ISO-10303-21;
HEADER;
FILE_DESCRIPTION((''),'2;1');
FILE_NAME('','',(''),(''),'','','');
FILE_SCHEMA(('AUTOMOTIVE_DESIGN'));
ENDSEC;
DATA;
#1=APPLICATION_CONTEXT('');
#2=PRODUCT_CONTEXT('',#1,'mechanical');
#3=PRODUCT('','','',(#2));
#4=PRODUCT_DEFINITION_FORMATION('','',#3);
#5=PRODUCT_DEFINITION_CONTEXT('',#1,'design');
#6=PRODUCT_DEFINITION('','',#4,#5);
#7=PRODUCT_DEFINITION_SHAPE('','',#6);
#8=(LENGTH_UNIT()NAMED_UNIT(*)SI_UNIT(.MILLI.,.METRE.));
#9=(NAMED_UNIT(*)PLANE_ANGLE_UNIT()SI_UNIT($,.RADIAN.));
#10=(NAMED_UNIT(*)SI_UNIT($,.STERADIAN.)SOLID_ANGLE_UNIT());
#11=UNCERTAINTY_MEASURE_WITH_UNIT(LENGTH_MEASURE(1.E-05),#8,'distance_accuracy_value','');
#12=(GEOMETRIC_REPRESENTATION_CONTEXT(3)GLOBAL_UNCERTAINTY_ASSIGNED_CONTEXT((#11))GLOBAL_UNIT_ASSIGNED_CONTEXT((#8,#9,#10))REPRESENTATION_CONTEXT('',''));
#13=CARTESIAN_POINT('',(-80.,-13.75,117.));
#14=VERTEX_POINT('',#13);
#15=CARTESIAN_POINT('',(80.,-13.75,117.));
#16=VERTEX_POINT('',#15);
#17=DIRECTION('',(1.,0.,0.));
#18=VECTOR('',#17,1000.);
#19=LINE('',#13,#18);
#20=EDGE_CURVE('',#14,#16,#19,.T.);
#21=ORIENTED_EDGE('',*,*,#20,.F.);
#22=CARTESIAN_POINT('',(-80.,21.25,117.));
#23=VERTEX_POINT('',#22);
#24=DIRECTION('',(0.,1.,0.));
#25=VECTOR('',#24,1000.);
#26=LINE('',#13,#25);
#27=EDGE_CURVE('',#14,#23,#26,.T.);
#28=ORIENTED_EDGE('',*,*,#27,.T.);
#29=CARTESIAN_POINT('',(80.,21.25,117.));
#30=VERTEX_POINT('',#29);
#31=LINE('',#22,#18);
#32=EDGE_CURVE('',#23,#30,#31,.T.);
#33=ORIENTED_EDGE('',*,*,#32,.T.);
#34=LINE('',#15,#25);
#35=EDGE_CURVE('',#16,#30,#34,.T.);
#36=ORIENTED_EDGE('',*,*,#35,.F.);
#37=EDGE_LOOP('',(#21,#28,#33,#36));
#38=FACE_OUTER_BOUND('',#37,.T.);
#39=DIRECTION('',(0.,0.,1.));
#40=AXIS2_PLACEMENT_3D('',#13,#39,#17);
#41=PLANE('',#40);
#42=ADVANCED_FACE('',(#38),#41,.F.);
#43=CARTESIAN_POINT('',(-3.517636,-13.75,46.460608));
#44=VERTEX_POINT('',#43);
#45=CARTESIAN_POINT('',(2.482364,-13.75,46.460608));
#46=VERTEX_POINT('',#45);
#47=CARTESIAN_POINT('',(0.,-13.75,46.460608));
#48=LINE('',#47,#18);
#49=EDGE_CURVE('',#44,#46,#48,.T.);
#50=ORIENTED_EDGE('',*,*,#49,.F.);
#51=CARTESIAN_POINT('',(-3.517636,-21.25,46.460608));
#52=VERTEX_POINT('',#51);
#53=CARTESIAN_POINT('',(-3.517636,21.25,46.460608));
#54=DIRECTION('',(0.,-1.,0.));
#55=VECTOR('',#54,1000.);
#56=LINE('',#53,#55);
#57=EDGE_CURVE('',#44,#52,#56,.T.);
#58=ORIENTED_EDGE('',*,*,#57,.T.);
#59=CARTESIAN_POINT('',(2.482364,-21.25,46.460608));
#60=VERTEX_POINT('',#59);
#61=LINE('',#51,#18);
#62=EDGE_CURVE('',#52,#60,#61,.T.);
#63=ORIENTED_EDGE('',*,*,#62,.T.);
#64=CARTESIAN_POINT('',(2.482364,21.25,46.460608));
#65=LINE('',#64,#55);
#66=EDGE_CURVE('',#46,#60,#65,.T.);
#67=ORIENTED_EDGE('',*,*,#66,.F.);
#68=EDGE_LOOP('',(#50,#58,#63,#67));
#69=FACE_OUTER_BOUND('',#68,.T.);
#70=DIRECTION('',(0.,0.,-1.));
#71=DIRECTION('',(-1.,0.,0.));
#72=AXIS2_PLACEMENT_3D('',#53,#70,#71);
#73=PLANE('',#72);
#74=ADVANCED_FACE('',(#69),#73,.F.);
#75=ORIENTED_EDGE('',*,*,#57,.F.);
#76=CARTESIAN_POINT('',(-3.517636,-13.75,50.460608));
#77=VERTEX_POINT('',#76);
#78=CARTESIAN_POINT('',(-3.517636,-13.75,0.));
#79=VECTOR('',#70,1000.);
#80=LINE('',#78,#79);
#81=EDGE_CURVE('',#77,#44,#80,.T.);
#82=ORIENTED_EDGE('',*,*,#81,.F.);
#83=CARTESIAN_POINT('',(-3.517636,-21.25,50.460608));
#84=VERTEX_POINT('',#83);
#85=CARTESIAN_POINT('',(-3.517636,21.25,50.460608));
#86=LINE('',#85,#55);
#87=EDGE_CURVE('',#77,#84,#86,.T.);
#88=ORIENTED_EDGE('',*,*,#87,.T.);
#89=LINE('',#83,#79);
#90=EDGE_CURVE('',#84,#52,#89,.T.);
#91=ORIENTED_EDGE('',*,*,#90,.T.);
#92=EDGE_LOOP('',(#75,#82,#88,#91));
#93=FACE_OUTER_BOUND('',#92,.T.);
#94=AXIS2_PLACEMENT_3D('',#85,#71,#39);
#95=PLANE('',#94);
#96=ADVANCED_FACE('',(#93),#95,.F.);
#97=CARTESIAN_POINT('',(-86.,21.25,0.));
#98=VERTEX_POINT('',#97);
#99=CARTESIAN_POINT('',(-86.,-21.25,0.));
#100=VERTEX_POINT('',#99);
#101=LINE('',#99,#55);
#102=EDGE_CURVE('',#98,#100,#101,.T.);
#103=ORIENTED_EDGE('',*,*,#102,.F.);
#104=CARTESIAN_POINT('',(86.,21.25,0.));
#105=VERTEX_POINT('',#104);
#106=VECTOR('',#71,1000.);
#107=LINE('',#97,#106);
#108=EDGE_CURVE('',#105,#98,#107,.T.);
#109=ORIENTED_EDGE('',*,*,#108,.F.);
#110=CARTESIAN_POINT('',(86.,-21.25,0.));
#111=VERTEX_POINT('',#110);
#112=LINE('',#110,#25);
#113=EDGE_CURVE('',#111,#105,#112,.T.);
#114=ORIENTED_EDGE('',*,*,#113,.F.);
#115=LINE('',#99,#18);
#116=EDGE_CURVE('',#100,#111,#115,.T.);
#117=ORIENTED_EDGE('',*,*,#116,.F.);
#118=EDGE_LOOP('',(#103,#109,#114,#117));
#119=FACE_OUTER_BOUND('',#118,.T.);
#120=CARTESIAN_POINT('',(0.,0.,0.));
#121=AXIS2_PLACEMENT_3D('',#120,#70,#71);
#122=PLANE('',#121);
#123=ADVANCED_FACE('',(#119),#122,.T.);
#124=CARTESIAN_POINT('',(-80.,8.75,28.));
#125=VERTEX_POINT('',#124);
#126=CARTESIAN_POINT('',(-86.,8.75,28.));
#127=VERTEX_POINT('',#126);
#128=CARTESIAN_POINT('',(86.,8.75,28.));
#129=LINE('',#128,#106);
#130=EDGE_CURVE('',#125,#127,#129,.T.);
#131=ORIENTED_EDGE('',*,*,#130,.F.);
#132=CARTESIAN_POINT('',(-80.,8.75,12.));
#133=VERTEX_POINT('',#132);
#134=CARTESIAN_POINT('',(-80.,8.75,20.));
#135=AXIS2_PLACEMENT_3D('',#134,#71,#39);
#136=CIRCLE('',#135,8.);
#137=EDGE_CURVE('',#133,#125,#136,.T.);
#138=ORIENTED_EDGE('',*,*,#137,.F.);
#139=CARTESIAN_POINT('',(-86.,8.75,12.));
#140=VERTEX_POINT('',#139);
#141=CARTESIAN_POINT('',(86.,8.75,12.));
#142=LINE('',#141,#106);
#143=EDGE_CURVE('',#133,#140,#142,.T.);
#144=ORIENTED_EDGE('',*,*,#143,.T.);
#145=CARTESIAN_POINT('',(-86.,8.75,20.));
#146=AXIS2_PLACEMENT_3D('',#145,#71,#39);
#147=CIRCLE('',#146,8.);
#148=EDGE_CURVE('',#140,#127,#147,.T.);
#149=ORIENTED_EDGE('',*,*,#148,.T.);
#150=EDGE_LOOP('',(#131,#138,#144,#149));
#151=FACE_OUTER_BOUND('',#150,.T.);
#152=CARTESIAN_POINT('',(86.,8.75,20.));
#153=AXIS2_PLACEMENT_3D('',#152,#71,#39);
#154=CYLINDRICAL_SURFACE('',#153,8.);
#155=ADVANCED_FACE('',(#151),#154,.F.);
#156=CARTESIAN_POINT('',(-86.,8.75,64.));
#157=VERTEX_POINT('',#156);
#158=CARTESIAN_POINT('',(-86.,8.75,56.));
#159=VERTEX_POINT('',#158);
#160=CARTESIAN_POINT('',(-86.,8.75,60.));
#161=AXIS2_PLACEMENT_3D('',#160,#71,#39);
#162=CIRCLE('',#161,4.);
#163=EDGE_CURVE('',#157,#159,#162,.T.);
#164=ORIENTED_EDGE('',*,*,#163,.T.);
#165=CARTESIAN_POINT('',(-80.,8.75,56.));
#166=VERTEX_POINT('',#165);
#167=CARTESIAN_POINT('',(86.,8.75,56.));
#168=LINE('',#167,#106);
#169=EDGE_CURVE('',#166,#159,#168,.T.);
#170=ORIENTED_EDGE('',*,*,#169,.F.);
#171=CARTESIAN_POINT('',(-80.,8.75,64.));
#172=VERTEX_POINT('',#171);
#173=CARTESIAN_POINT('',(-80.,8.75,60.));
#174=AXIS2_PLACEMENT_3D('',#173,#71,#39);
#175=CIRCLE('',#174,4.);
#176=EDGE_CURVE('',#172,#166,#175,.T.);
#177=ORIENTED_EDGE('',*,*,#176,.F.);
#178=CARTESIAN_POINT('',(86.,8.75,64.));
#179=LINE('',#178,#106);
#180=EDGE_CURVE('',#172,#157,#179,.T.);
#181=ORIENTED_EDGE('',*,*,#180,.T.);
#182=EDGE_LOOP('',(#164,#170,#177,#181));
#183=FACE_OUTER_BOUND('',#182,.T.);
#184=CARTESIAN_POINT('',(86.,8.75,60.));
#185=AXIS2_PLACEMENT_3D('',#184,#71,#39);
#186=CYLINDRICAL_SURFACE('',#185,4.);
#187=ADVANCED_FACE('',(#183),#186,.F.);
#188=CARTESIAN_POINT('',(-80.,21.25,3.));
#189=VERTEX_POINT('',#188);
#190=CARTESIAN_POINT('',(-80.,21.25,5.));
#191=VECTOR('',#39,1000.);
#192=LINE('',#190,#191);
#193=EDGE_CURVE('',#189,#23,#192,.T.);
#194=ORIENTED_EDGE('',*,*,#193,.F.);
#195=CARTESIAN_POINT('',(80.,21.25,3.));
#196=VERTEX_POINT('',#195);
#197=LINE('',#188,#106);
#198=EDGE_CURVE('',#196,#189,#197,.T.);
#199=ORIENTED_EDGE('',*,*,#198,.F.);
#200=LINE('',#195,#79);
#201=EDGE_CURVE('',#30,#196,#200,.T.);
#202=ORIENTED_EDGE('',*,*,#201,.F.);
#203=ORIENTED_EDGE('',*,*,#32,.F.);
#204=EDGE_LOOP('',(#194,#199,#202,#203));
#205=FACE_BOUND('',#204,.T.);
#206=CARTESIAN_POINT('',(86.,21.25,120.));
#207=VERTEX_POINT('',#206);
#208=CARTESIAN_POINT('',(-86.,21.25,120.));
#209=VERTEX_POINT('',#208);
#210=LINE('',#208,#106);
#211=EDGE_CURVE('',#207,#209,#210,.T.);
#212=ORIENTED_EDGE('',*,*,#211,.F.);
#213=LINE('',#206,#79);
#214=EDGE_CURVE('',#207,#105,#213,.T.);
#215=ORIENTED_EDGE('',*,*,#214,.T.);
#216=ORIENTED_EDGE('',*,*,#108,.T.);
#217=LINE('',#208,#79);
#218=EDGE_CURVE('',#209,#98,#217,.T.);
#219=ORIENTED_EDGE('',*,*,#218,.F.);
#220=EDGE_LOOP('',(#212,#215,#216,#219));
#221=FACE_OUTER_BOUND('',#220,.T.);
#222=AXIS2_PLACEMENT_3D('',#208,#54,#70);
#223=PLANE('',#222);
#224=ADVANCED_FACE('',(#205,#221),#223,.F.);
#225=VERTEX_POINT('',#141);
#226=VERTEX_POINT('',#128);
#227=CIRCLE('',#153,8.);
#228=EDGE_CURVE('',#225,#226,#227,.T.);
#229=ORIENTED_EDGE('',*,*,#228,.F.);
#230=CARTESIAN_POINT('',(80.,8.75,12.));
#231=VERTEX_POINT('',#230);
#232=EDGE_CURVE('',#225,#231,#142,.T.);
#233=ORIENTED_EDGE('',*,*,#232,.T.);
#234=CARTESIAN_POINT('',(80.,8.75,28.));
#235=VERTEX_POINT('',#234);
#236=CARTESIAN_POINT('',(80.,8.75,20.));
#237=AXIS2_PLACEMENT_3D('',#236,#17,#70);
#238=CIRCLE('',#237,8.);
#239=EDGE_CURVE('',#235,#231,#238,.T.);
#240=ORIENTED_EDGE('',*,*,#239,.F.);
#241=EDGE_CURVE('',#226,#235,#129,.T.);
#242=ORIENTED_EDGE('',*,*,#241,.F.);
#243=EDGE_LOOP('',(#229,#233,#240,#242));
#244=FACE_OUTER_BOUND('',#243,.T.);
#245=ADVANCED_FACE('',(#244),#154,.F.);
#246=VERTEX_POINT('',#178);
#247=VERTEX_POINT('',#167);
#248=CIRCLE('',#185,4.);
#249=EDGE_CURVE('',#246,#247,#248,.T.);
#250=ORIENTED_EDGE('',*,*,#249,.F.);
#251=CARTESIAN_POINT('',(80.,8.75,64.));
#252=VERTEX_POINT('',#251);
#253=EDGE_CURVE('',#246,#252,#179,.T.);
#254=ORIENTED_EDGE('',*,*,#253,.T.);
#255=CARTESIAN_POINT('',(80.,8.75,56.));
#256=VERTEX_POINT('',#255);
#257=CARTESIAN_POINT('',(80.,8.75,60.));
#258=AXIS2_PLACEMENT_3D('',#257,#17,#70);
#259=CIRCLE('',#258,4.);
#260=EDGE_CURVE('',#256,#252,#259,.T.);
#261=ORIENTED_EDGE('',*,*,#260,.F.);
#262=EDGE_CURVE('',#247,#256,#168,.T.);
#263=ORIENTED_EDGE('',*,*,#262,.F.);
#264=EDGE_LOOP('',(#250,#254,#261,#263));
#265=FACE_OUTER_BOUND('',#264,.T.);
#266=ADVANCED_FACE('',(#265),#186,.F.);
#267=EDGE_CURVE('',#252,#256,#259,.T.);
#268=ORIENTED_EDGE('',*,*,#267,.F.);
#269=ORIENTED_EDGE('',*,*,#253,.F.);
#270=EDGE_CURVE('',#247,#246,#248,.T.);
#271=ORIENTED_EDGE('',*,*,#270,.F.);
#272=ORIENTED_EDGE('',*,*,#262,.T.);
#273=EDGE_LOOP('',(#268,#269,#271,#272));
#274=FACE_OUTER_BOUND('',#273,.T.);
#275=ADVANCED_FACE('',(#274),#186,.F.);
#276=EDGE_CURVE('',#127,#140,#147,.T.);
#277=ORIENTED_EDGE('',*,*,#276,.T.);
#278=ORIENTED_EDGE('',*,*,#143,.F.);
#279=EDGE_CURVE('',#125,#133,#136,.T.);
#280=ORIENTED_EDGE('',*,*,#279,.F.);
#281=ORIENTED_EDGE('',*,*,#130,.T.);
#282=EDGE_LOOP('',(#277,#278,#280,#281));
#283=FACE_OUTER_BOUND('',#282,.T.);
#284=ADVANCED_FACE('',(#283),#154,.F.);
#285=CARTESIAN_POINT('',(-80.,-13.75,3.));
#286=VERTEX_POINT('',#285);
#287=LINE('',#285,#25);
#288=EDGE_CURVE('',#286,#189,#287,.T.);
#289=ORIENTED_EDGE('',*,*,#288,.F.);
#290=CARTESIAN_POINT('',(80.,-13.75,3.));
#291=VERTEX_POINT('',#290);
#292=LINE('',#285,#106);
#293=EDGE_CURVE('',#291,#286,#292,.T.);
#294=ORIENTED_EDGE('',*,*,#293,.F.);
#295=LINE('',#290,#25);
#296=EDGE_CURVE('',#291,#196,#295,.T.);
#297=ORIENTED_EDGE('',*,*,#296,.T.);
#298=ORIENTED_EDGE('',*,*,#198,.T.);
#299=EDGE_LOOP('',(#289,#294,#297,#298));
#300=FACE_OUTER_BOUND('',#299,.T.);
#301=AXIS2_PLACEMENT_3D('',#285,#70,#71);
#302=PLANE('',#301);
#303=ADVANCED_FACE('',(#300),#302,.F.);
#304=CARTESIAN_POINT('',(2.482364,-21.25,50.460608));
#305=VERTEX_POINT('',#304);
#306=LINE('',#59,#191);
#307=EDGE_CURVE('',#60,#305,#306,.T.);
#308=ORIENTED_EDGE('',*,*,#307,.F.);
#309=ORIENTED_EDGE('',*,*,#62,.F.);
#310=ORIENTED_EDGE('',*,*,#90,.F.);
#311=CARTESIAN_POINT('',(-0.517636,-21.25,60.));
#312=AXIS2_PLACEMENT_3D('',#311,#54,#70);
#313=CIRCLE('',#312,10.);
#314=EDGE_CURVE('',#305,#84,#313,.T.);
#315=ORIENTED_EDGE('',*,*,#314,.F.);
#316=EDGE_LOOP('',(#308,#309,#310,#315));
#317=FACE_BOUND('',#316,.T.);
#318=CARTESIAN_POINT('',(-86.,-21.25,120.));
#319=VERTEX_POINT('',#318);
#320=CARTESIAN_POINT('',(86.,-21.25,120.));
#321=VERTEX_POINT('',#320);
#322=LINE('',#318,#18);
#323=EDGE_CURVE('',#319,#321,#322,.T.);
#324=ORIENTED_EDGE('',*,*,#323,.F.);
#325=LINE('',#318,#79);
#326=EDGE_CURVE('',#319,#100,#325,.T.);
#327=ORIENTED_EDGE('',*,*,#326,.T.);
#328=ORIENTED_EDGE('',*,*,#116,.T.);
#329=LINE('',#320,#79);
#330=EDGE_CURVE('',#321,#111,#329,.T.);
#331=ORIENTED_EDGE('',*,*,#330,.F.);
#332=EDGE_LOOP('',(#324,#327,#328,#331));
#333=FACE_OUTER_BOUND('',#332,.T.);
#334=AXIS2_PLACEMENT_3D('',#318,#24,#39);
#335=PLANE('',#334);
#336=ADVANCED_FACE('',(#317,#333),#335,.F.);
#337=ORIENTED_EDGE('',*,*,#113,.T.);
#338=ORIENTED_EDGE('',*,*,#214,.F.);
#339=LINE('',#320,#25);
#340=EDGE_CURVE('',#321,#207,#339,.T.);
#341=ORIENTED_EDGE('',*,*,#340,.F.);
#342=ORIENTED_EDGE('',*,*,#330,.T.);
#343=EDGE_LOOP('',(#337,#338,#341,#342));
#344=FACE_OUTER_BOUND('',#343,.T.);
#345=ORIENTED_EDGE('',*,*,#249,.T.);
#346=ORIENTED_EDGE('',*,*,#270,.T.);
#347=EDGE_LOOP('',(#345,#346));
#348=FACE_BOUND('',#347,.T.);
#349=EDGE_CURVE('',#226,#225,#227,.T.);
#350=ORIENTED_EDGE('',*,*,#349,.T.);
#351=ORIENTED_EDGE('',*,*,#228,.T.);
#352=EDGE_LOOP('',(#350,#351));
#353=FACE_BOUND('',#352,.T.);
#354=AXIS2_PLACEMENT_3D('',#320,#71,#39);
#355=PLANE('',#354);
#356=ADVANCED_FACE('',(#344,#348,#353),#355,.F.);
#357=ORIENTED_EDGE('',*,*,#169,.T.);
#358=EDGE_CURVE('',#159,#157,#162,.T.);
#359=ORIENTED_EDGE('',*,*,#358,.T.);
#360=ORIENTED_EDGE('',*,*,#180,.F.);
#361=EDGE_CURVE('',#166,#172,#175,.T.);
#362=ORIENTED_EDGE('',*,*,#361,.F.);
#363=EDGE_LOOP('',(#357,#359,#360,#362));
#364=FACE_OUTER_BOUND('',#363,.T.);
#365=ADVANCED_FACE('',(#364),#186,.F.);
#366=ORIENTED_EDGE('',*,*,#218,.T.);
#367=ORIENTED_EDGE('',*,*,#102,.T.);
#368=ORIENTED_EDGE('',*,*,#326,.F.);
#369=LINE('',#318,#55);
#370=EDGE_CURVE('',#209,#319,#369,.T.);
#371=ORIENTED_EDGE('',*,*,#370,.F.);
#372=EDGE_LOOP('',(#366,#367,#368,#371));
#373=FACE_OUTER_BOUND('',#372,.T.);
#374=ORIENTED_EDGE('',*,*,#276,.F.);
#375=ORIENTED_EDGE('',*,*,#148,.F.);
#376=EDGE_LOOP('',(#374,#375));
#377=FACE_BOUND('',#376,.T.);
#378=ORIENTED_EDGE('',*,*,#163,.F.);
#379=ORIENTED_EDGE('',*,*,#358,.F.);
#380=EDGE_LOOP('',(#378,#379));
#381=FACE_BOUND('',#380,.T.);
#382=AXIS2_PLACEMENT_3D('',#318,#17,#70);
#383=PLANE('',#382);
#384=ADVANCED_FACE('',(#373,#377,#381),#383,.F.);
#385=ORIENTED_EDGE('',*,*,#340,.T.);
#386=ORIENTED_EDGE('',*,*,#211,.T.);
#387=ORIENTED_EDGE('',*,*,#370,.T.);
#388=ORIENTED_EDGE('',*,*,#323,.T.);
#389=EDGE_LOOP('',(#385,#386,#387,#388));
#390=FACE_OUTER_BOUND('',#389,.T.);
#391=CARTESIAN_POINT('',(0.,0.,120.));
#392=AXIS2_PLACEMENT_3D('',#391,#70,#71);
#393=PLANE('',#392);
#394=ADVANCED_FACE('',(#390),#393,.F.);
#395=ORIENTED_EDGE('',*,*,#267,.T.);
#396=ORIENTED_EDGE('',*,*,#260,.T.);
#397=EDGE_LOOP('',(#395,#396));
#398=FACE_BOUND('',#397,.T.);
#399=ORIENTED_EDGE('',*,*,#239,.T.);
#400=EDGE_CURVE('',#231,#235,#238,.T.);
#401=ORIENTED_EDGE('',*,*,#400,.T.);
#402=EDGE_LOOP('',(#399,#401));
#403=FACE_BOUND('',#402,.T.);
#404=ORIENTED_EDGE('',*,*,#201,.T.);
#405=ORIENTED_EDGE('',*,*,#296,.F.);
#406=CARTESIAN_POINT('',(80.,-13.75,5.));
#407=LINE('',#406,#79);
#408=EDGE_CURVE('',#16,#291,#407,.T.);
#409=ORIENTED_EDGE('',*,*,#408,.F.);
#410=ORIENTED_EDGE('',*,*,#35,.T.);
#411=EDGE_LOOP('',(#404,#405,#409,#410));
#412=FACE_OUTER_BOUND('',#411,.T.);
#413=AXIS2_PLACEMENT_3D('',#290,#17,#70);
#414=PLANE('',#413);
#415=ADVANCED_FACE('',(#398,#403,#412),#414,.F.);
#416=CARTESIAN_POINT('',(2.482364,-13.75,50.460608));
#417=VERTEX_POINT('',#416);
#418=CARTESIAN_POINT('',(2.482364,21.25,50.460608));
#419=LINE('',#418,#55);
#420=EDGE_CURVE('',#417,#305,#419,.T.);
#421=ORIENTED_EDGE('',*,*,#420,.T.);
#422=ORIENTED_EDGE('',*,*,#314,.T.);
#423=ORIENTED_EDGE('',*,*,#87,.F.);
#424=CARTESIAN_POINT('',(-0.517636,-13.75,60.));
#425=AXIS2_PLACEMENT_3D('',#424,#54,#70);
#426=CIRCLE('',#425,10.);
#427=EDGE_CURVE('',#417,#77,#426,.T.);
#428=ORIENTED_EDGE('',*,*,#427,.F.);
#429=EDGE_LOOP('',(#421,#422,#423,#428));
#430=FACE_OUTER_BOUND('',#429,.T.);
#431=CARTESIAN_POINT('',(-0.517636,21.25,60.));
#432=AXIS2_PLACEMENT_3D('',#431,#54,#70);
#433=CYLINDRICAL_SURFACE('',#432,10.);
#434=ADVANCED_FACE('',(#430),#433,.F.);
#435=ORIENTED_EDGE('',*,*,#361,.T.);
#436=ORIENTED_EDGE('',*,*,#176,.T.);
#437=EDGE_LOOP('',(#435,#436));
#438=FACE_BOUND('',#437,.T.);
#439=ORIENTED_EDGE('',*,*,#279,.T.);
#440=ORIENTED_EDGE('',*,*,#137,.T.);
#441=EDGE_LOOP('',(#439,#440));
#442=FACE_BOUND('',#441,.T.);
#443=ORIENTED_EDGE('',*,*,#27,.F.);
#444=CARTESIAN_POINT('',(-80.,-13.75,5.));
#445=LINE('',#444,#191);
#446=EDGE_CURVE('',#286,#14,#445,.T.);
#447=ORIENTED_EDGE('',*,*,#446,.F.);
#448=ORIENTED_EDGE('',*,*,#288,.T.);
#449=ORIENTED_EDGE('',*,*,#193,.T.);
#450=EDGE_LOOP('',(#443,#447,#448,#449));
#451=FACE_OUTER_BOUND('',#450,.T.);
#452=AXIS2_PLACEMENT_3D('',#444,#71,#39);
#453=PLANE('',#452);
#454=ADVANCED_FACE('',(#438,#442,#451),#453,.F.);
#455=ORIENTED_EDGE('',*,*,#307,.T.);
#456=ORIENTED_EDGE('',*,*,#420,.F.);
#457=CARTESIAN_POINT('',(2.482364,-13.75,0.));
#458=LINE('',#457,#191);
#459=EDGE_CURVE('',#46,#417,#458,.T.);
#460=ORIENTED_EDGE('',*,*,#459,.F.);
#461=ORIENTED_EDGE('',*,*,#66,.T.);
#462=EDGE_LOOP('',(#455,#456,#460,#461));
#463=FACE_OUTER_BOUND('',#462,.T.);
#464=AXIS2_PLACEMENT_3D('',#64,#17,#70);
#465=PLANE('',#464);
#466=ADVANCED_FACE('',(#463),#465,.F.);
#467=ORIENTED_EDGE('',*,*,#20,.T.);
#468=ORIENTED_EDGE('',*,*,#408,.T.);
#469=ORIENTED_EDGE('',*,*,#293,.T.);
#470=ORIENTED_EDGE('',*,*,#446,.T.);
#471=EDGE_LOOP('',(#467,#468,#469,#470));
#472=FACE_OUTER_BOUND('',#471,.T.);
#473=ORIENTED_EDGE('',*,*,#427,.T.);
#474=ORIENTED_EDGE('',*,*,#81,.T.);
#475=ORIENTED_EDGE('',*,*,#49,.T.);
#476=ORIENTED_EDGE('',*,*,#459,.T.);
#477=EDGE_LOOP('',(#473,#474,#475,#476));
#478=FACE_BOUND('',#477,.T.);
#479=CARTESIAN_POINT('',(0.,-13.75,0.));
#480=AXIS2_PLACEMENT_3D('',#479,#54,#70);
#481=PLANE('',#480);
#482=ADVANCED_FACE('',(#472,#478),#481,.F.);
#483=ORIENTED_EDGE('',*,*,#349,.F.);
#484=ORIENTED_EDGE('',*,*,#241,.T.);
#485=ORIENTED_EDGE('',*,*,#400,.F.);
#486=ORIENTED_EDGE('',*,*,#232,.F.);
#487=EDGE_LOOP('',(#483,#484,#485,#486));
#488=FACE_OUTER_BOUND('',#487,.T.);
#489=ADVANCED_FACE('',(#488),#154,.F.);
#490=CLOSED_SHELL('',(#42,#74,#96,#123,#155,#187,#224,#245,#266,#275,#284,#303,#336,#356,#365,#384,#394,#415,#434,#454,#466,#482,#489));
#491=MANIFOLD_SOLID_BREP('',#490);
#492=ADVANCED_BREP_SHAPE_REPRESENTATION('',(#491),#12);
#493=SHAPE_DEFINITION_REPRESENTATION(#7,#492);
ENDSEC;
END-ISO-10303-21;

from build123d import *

# Parameters (mm, degrees)
SKETCH_1_W          = 172
SKETCH_1_H          = 42.5
EXTRUDE_2_DEPTH     = 120
CUT_EXTRUDE_1_DEPTH = 35
SKETCH_5_R          = 8
SKETCH_5_R_2        = 4
CUT_EXTRUDE_2_DEPTH = 211.797444244
CUT_EXTRUDE_4_DEPTH = 154.630237909


with BuildPart() as part:
    # 草图1 → 凸台-拉伸2 (new body)
    with BuildSketch(Plane.XY):
        Rectangle(SKETCH_1_W, SKETCH_1_H)
    extrude(amount=EXTRUDE_2_DEPTH)

    # 草图2 → 切除-拉伸1 (cut)
    with BuildSketch(Plane(origin=(0, 21.25, 0), x_dir=(1, 0, 0), z_dir=(0, 1, 0))):
        Polygon((-80, -5), (-80, -3), (80, -3), (80, -5), (80, -117), (-80, -117), align=None)
    extrude(amount=-CUT_EXTRUDE_1_DEPTH, mode=Mode.SUBTRACT)

    # 草图5 → 切除-拉伸2 (cut, through all)
    with BuildSketch(Plane.ZY.offset(86)):
        with Locations((20, 8.75)):
            Circle(SKETCH_5_R)
        with Locations((60, 8.75)):
            Circle(SKETCH_5_R_2)
    extrude(amount=-CUT_EXTRUDE_2_DEPTH, mode=Mode.SUBTRACT)

    # 草图6 → 切除-拉伸4 (cut, through all)
    with BuildSketch(Plane.XZ.offset(21.25)):
        with BuildLine():
            Line((-3.517636002, 50.460607986), (-3.517636002, 46.460607986))
            Line((-3.517636002, 46.460607986), (2.482363998, 46.460607986))
            Line((2.482363998, 46.460607986), (2.482363998, 50.460607986))
            ThreePointArc((2.482363998, 50.460607986), (-0.517636002, 70), (-3.517636002, 50.460607986))
        make_face()
    extrude(amount=-CUT_EXTRUDE_4_DEPTH, mode=Mode.SUBTRACT)


solid = part.part
